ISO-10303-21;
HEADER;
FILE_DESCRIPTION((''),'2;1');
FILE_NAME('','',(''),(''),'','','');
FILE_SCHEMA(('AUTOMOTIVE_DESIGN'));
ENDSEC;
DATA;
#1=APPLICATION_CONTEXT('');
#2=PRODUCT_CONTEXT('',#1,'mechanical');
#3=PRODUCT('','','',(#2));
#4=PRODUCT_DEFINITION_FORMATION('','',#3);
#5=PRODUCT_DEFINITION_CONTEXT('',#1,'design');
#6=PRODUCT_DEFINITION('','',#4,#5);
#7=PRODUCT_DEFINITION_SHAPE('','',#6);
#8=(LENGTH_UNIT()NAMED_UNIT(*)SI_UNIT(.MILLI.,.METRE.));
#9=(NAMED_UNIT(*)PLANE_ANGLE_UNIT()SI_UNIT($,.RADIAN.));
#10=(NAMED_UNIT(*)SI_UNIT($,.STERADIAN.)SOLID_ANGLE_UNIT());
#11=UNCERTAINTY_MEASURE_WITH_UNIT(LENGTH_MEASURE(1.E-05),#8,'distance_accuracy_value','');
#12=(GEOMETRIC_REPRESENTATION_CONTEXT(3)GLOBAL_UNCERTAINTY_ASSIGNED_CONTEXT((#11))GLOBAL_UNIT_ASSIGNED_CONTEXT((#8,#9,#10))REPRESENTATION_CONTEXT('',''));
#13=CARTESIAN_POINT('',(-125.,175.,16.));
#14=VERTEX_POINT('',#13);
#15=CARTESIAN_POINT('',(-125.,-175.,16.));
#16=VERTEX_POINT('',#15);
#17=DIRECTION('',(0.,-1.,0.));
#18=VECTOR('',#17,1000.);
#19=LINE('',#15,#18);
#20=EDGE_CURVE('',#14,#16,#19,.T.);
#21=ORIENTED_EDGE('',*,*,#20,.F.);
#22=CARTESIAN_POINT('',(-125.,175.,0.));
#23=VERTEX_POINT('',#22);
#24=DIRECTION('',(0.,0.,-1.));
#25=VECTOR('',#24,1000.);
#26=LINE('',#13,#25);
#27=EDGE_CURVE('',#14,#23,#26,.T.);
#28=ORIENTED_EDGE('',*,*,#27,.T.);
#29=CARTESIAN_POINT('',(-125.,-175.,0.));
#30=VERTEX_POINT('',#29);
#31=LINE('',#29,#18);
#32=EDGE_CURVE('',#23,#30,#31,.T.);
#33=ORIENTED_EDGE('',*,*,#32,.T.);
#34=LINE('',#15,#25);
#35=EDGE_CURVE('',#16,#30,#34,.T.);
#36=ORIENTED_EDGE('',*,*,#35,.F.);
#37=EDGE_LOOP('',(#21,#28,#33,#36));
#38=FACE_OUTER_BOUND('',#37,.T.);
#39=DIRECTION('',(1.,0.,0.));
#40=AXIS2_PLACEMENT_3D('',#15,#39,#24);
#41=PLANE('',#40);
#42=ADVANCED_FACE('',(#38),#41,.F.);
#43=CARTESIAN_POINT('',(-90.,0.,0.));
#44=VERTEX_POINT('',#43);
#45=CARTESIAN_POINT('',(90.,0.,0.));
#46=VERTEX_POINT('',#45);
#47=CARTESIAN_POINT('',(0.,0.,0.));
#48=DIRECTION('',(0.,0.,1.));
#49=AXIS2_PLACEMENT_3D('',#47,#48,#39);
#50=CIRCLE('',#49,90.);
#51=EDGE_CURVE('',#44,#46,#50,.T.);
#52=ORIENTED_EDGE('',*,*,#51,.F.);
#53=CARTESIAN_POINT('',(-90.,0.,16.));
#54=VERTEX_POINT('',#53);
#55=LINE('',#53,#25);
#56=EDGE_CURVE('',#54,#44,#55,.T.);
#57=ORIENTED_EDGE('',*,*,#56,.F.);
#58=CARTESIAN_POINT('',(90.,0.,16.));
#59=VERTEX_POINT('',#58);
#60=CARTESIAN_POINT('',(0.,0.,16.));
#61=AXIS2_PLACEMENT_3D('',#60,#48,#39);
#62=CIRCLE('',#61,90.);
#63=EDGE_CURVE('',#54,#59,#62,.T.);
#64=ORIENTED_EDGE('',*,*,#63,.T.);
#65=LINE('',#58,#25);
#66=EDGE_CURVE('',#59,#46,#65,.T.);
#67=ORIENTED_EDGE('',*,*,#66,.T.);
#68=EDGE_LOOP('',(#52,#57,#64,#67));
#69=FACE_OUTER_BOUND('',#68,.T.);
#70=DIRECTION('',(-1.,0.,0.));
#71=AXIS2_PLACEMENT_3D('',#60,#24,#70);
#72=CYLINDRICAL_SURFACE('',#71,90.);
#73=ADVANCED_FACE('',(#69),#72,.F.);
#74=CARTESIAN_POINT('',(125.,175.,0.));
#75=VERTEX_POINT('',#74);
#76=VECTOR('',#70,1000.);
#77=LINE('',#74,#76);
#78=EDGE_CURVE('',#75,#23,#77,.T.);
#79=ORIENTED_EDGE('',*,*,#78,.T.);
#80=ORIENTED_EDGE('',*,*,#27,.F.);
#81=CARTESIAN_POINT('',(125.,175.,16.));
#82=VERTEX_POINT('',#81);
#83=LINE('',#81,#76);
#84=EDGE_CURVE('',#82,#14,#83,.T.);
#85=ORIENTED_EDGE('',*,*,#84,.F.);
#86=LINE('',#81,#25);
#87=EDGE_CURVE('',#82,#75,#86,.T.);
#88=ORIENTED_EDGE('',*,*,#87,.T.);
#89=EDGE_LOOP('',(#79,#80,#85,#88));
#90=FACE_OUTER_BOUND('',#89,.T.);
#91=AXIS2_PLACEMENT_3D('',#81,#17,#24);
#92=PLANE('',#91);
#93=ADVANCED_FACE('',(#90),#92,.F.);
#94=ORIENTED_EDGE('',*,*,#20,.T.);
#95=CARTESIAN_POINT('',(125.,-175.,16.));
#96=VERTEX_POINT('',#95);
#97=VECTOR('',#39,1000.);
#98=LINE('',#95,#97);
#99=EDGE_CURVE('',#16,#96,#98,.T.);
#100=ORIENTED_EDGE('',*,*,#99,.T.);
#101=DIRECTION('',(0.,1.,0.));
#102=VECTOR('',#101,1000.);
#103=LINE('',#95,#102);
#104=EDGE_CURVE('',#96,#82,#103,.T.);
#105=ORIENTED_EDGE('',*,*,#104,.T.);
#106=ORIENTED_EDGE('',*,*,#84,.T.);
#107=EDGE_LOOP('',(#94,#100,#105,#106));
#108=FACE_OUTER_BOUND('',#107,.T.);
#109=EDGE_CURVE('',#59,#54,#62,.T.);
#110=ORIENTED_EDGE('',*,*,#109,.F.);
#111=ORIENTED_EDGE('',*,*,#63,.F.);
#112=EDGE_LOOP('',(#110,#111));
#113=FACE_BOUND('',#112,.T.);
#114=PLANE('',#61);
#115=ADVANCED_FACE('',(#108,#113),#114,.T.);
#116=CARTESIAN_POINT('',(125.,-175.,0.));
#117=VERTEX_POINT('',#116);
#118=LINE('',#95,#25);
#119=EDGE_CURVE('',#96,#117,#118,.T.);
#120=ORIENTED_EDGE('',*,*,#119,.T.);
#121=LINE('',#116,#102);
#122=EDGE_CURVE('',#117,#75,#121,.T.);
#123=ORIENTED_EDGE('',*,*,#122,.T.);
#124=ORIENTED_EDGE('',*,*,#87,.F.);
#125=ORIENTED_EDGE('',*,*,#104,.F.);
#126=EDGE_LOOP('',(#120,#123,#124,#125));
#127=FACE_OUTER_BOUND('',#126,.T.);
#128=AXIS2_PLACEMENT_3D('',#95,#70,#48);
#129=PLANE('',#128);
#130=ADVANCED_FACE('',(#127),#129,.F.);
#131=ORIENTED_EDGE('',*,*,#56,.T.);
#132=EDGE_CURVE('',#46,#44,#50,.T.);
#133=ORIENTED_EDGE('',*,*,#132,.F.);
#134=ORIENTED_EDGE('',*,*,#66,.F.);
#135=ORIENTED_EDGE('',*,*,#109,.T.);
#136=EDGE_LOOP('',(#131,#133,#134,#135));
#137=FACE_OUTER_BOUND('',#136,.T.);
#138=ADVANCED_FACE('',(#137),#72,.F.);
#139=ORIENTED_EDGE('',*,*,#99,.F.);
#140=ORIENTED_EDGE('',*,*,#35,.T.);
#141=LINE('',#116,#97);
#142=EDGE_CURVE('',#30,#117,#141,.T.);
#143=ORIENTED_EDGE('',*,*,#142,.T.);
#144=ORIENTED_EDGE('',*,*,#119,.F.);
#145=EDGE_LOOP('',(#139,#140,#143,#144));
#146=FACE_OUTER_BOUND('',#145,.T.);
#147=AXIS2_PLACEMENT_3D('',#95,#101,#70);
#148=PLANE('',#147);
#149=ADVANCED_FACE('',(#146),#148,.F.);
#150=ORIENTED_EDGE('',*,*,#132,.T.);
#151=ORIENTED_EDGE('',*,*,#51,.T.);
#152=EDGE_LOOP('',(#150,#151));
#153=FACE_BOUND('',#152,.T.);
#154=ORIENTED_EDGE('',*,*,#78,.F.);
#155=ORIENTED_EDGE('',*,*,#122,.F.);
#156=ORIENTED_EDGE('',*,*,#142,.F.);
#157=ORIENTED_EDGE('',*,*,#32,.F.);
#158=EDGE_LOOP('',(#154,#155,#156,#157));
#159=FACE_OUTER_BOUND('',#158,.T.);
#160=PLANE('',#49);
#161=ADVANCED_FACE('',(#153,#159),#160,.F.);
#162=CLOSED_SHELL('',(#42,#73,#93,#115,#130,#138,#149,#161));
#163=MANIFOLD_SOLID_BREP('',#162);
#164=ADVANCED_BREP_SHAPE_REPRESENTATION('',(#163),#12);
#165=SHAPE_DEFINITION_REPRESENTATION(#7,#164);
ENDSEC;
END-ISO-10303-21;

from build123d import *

# Parameters (mm, degrees)
SKETCH_1_W      = 250
SKETCH_1_H      = 350
SKETCH_1_R      = 90
EXTRUDE_1_DEPTH = 16


with BuildPart() as part:
    # 草图1 → 凸台-拉伸1 (new body)
    with BuildSketch(Plane.XY):
        Rectangle(SKETCH_1_W, SKETCH_1_H)
        Circle(SKETCH_1_R, mode=Mode.SUBTRACT)
    extrude(amount=EXTRUDE_1_DEPTH)


solid = part.part
